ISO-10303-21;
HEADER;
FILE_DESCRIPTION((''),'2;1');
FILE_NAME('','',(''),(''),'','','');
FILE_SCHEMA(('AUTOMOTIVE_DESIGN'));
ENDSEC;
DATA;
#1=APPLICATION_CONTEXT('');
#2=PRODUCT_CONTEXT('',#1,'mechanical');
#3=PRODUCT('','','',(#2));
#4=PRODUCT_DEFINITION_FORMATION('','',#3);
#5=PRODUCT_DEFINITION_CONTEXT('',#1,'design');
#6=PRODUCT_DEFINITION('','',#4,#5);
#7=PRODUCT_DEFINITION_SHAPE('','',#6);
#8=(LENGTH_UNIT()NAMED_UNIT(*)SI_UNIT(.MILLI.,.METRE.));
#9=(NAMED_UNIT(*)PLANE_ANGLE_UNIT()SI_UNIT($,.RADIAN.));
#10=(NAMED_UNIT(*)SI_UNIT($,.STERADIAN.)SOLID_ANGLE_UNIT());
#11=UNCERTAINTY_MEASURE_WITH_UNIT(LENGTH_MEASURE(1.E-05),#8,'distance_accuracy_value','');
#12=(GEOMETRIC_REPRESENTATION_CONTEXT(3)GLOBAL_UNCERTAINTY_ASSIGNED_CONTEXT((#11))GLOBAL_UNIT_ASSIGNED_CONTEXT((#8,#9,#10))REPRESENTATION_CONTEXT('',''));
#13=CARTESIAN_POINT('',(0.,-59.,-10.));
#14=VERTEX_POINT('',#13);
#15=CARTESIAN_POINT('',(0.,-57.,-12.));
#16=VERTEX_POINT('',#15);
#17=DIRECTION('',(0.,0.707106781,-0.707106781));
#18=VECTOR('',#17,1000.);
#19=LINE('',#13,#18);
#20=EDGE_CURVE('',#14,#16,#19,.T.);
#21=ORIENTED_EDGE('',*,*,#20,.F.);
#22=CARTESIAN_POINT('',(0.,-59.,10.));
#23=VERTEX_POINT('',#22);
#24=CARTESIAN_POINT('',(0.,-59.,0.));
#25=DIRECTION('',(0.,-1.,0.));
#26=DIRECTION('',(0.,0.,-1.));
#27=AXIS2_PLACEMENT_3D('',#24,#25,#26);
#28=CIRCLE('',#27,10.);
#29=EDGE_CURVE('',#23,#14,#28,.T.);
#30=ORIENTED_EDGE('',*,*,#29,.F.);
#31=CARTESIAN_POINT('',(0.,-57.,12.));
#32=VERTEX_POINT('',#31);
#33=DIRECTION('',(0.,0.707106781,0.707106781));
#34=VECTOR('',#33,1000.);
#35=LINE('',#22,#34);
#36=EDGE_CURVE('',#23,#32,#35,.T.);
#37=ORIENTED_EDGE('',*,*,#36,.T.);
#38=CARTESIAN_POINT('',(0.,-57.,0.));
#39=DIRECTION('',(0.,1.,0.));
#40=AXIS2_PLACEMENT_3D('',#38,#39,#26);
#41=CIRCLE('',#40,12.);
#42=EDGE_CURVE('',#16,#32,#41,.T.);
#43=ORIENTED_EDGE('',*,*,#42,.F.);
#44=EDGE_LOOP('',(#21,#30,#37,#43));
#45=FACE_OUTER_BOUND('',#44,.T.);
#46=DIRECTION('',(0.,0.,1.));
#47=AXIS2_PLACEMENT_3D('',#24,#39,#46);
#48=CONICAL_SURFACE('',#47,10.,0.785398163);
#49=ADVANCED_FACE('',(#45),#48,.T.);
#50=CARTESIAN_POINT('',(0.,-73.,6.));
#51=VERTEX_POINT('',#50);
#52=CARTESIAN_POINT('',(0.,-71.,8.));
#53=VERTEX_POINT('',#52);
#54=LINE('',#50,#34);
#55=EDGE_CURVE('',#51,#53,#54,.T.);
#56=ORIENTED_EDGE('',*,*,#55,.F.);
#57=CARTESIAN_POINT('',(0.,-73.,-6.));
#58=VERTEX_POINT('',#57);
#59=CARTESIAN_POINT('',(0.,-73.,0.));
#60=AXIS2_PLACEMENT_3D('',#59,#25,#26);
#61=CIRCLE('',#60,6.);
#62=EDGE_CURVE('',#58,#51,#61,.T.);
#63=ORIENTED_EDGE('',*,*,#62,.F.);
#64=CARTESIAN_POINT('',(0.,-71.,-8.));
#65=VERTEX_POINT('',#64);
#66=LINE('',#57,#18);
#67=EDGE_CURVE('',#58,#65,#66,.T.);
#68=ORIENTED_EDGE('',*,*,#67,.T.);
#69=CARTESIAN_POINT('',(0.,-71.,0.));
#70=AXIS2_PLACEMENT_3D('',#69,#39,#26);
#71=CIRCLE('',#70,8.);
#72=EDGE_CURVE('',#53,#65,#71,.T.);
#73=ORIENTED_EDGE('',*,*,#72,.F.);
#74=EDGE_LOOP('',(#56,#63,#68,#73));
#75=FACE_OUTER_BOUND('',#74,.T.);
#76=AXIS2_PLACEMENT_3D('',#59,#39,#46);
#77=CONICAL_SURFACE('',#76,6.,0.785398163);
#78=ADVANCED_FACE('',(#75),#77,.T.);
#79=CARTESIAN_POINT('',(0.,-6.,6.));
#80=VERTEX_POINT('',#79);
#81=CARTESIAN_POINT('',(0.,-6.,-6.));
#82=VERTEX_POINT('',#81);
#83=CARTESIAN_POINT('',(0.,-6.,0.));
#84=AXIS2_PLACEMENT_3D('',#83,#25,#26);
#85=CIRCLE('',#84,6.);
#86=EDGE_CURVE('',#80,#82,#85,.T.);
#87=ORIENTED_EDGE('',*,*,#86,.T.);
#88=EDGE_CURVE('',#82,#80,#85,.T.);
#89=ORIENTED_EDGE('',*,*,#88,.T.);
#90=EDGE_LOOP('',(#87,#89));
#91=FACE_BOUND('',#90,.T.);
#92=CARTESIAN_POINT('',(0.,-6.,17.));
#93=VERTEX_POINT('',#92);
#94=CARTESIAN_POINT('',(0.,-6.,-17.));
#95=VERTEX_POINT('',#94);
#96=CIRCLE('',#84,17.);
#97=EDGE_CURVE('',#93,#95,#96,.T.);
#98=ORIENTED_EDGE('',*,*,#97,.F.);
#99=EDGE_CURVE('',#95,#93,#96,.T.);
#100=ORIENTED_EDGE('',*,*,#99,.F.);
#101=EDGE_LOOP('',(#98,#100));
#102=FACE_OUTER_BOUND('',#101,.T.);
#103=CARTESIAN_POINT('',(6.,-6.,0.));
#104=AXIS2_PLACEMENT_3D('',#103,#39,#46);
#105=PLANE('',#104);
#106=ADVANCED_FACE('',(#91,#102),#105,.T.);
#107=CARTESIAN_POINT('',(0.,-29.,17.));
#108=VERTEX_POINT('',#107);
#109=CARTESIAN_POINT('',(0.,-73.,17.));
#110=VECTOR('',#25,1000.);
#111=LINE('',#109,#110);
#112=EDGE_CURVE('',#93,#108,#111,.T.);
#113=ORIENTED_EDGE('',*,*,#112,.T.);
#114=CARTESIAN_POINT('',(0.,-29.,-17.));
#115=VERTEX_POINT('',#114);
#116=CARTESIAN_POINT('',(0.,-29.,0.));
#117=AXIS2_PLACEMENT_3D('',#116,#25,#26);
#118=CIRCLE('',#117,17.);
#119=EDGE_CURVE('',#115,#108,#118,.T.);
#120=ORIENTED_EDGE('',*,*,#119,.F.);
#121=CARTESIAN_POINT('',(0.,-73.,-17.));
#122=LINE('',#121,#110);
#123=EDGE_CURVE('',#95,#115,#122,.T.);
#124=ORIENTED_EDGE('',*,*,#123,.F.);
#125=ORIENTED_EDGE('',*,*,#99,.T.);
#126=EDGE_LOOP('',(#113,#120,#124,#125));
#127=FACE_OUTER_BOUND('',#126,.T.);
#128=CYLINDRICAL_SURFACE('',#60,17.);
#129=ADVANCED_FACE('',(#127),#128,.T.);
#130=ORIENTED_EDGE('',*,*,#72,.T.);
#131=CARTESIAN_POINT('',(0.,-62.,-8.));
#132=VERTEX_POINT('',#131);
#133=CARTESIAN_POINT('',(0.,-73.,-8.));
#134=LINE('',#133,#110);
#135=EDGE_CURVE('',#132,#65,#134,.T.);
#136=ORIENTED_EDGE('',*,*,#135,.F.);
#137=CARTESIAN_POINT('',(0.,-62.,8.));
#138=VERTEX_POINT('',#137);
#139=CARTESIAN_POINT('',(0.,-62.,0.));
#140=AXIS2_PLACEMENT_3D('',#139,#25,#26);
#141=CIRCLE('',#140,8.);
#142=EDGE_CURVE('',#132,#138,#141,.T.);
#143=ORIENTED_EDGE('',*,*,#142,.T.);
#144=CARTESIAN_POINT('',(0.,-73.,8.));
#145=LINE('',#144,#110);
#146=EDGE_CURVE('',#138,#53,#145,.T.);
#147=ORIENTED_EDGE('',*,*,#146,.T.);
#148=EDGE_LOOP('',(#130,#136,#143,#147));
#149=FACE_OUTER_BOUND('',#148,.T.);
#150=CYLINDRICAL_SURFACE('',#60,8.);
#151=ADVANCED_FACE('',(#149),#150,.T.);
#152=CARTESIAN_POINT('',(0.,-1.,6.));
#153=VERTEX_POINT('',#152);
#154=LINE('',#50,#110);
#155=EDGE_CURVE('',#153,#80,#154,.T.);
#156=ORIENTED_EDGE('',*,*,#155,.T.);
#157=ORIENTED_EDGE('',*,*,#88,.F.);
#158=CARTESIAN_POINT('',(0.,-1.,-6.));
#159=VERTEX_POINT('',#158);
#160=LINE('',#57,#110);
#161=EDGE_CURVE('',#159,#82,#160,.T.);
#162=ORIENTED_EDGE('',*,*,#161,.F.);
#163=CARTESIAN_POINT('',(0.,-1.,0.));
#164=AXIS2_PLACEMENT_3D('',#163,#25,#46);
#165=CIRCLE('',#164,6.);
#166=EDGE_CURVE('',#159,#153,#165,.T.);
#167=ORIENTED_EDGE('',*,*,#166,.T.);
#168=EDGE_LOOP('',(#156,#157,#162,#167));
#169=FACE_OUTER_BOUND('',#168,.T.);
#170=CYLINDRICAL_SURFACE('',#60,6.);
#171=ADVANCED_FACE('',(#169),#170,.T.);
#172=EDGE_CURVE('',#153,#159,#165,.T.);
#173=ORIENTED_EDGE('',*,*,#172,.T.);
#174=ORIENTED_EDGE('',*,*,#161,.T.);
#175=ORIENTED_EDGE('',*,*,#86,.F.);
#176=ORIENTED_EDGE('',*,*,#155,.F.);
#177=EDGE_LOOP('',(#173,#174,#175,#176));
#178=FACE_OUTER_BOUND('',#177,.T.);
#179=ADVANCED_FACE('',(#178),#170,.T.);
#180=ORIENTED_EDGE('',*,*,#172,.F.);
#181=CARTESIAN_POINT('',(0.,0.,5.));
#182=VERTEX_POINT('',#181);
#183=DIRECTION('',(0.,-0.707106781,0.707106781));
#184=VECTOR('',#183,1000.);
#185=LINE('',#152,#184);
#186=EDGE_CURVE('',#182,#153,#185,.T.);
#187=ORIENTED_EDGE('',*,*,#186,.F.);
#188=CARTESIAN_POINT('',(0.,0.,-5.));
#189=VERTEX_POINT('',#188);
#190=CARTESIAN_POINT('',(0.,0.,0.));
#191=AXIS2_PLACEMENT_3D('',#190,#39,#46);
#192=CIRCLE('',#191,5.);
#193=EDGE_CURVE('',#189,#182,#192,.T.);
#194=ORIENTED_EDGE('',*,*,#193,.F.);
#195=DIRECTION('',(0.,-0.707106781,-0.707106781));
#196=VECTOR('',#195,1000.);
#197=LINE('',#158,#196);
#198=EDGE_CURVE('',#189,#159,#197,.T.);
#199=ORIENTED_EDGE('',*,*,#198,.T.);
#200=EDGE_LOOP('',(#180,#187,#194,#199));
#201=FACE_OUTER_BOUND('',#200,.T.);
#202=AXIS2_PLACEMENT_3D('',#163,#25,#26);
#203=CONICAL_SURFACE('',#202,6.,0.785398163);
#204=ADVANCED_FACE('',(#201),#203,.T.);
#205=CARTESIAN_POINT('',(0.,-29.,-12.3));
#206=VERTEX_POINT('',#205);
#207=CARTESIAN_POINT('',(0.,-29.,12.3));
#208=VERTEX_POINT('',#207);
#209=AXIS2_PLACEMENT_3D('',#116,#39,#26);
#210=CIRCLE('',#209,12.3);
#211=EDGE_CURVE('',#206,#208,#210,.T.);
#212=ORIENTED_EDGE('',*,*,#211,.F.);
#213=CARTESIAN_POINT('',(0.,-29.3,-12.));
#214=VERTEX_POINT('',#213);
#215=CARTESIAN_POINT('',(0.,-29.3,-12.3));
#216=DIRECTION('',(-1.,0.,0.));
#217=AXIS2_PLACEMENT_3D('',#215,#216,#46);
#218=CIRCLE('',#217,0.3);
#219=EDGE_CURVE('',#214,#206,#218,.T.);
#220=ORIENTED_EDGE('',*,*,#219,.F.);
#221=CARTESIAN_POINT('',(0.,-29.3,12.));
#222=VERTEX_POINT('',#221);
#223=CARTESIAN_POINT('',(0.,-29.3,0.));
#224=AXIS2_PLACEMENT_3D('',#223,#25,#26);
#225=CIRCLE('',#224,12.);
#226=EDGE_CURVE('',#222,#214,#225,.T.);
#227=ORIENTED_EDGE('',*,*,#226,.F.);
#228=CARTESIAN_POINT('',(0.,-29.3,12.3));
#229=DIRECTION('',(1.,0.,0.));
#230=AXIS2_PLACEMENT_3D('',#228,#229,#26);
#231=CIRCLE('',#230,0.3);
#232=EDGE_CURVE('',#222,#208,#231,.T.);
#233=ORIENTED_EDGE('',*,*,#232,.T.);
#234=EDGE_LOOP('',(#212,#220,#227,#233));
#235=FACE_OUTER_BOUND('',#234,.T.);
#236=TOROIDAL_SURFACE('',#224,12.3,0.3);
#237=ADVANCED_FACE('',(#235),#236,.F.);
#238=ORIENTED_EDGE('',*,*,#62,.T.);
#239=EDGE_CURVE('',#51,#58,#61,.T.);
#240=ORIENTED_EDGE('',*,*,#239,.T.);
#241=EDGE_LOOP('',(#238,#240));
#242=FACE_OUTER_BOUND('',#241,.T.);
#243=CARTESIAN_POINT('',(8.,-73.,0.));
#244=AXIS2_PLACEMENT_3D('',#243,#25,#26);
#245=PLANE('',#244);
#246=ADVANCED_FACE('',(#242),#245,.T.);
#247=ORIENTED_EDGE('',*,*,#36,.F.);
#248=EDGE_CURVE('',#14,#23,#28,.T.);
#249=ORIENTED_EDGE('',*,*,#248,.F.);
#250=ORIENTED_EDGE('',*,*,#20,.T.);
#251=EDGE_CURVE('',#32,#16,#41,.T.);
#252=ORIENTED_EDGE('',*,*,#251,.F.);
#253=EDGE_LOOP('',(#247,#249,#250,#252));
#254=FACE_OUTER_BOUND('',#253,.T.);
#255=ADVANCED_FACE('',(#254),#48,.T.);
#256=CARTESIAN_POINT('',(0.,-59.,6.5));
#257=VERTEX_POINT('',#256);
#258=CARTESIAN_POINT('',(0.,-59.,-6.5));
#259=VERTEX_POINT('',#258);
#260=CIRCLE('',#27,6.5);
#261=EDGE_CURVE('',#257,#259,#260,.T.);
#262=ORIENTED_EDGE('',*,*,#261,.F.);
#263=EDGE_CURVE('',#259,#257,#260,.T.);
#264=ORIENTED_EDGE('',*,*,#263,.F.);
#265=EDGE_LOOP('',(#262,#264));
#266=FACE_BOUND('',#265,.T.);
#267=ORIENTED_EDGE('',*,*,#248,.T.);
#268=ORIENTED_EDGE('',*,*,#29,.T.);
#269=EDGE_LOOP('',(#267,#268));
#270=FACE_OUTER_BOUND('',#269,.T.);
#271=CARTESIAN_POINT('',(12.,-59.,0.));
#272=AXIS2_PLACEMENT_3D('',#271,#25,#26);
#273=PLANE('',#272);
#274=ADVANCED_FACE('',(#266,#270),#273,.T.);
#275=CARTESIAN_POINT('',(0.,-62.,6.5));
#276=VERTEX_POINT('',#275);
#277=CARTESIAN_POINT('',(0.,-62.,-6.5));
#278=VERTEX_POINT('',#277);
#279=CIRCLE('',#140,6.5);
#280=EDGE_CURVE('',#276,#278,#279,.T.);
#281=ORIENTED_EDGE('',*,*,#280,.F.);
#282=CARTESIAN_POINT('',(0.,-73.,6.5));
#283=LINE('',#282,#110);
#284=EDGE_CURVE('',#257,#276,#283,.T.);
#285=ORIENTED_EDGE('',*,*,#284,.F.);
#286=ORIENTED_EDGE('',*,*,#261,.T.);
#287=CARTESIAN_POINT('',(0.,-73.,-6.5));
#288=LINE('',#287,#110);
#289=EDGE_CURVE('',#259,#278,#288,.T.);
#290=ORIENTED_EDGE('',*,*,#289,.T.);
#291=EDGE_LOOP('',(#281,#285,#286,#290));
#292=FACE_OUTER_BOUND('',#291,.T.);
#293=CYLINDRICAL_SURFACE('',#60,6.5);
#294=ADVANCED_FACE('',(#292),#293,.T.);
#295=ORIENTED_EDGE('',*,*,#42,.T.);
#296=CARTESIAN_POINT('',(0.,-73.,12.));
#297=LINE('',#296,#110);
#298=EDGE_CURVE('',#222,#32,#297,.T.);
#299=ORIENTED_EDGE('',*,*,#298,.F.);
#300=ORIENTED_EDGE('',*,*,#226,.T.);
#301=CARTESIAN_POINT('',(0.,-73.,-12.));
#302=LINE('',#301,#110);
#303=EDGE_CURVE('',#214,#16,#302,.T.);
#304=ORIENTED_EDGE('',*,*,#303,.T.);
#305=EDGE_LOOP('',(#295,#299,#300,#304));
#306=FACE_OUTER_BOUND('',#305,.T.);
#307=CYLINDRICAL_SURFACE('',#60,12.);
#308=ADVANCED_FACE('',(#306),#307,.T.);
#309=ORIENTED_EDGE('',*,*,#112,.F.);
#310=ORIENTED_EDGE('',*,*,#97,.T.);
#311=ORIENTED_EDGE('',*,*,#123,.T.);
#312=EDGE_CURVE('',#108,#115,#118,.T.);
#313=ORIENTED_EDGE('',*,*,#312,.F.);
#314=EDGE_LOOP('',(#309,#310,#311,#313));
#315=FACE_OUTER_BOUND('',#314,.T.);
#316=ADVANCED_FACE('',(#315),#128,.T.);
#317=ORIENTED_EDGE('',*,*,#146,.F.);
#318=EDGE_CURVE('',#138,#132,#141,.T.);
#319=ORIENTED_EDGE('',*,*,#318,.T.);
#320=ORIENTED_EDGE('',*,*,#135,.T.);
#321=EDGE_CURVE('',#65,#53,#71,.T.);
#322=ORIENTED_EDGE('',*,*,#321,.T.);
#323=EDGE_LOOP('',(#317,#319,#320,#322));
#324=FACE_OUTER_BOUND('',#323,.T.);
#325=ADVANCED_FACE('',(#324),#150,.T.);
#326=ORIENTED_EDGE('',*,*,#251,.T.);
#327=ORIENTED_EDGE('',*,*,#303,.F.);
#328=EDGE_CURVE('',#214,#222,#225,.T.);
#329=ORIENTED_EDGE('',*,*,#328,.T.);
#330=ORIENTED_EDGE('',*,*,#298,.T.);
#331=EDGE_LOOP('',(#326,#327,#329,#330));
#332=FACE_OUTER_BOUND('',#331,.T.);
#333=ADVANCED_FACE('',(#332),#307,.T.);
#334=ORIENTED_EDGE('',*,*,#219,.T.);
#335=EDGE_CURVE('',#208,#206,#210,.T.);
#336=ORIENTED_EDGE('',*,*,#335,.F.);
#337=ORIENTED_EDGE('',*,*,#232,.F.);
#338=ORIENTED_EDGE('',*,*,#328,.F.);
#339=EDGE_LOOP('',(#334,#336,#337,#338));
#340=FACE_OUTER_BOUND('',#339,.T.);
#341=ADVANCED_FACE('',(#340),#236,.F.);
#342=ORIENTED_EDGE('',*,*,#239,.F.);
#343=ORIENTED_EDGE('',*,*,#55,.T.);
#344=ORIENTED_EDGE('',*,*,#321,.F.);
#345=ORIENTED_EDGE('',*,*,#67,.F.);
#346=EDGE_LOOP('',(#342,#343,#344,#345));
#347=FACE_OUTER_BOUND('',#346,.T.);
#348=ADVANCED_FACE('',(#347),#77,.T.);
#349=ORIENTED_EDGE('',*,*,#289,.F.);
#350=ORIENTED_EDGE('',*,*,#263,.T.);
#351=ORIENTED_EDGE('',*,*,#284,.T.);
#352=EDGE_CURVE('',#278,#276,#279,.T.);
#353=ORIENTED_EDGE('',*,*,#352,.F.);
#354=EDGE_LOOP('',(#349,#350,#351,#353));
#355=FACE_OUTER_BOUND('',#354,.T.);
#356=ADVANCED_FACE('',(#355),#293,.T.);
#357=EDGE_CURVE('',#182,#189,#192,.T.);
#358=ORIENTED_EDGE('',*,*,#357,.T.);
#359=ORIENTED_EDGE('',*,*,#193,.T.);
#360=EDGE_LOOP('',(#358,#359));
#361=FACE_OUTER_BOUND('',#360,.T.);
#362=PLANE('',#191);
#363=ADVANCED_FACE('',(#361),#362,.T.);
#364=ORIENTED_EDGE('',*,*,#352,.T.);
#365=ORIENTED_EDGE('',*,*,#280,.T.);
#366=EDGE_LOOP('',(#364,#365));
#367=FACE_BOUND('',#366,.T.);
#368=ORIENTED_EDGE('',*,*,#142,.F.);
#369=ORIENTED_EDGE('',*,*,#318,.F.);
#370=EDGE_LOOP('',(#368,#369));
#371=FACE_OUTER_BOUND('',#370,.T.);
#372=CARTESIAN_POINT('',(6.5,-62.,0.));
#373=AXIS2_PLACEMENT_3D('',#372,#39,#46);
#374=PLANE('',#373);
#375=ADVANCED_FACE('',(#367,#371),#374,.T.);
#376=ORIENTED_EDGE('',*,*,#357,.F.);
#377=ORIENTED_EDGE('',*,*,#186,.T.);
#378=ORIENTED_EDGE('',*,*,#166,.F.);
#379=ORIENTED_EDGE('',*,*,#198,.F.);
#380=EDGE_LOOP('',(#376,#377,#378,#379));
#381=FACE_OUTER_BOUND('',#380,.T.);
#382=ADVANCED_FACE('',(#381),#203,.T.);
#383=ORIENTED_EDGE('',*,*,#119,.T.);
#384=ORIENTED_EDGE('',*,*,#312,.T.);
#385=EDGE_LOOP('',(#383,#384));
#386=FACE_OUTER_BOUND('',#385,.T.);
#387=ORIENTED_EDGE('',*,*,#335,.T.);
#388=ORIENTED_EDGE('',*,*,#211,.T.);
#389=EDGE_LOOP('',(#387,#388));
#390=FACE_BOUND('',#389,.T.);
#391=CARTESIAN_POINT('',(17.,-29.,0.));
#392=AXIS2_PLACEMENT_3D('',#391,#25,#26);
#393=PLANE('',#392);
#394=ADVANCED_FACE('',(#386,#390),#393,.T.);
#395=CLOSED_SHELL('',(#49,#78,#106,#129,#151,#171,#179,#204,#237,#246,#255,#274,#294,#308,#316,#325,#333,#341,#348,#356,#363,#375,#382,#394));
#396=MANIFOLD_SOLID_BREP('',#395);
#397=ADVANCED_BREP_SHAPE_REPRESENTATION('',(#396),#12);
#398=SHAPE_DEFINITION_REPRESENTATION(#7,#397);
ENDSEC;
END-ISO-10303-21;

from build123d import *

# Parameters (mm, degrees)
CHAMFER_1_SIZE = 2
CHAMFER_2_SIZE = 1
FILLET_1_R     = 0.3


with BuildPart() as part:
    # 草图1 → 旋转1 (revolve)
    with BuildSketch(Plane.XY, mode=Mode.PRIVATE) as revolve_1_sk:
        Polygon((0, 0), (6, 0), (6, -6), (17, -6), (17, -29), (12, -29), (12, -59), (6.5, -59), (6.5, -62), (8, -62), (8, -73), (0, -73), align=None)
    revolve(revolve_1_sk.sketch.rotate(Axis((0, -73, 0), (0, 1, 0)), 90), axis=Axis((0, -73, 0), (0, 1, 0)))

    # 倒角1
    chamfer_1_edges = [part.edges().sort_by_distance(p)[0] for p in [
        (0, -59, 12),
        (0, -73, 8),
    ]]
    chamfer(chamfer_1_edges, length=CHAMFER_1_SIZE)

    # 倒角2
    chamfer_2_edges = [part.edges().sort_by_distance(p)[0] for p in [
        (0, 0, 6),
    ]]
    chamfer(chamfer_2_edges, length=CHAMFER_2_SIZE)

    # 圆角1
    fillet_1_edges = [part.edges().sort_by_distance(p)[0] for p in [
        (0, -29, 12),
    ]]
    fillet(fillet_1_edges, radius=FILLET_1_R)


solid = part.part
